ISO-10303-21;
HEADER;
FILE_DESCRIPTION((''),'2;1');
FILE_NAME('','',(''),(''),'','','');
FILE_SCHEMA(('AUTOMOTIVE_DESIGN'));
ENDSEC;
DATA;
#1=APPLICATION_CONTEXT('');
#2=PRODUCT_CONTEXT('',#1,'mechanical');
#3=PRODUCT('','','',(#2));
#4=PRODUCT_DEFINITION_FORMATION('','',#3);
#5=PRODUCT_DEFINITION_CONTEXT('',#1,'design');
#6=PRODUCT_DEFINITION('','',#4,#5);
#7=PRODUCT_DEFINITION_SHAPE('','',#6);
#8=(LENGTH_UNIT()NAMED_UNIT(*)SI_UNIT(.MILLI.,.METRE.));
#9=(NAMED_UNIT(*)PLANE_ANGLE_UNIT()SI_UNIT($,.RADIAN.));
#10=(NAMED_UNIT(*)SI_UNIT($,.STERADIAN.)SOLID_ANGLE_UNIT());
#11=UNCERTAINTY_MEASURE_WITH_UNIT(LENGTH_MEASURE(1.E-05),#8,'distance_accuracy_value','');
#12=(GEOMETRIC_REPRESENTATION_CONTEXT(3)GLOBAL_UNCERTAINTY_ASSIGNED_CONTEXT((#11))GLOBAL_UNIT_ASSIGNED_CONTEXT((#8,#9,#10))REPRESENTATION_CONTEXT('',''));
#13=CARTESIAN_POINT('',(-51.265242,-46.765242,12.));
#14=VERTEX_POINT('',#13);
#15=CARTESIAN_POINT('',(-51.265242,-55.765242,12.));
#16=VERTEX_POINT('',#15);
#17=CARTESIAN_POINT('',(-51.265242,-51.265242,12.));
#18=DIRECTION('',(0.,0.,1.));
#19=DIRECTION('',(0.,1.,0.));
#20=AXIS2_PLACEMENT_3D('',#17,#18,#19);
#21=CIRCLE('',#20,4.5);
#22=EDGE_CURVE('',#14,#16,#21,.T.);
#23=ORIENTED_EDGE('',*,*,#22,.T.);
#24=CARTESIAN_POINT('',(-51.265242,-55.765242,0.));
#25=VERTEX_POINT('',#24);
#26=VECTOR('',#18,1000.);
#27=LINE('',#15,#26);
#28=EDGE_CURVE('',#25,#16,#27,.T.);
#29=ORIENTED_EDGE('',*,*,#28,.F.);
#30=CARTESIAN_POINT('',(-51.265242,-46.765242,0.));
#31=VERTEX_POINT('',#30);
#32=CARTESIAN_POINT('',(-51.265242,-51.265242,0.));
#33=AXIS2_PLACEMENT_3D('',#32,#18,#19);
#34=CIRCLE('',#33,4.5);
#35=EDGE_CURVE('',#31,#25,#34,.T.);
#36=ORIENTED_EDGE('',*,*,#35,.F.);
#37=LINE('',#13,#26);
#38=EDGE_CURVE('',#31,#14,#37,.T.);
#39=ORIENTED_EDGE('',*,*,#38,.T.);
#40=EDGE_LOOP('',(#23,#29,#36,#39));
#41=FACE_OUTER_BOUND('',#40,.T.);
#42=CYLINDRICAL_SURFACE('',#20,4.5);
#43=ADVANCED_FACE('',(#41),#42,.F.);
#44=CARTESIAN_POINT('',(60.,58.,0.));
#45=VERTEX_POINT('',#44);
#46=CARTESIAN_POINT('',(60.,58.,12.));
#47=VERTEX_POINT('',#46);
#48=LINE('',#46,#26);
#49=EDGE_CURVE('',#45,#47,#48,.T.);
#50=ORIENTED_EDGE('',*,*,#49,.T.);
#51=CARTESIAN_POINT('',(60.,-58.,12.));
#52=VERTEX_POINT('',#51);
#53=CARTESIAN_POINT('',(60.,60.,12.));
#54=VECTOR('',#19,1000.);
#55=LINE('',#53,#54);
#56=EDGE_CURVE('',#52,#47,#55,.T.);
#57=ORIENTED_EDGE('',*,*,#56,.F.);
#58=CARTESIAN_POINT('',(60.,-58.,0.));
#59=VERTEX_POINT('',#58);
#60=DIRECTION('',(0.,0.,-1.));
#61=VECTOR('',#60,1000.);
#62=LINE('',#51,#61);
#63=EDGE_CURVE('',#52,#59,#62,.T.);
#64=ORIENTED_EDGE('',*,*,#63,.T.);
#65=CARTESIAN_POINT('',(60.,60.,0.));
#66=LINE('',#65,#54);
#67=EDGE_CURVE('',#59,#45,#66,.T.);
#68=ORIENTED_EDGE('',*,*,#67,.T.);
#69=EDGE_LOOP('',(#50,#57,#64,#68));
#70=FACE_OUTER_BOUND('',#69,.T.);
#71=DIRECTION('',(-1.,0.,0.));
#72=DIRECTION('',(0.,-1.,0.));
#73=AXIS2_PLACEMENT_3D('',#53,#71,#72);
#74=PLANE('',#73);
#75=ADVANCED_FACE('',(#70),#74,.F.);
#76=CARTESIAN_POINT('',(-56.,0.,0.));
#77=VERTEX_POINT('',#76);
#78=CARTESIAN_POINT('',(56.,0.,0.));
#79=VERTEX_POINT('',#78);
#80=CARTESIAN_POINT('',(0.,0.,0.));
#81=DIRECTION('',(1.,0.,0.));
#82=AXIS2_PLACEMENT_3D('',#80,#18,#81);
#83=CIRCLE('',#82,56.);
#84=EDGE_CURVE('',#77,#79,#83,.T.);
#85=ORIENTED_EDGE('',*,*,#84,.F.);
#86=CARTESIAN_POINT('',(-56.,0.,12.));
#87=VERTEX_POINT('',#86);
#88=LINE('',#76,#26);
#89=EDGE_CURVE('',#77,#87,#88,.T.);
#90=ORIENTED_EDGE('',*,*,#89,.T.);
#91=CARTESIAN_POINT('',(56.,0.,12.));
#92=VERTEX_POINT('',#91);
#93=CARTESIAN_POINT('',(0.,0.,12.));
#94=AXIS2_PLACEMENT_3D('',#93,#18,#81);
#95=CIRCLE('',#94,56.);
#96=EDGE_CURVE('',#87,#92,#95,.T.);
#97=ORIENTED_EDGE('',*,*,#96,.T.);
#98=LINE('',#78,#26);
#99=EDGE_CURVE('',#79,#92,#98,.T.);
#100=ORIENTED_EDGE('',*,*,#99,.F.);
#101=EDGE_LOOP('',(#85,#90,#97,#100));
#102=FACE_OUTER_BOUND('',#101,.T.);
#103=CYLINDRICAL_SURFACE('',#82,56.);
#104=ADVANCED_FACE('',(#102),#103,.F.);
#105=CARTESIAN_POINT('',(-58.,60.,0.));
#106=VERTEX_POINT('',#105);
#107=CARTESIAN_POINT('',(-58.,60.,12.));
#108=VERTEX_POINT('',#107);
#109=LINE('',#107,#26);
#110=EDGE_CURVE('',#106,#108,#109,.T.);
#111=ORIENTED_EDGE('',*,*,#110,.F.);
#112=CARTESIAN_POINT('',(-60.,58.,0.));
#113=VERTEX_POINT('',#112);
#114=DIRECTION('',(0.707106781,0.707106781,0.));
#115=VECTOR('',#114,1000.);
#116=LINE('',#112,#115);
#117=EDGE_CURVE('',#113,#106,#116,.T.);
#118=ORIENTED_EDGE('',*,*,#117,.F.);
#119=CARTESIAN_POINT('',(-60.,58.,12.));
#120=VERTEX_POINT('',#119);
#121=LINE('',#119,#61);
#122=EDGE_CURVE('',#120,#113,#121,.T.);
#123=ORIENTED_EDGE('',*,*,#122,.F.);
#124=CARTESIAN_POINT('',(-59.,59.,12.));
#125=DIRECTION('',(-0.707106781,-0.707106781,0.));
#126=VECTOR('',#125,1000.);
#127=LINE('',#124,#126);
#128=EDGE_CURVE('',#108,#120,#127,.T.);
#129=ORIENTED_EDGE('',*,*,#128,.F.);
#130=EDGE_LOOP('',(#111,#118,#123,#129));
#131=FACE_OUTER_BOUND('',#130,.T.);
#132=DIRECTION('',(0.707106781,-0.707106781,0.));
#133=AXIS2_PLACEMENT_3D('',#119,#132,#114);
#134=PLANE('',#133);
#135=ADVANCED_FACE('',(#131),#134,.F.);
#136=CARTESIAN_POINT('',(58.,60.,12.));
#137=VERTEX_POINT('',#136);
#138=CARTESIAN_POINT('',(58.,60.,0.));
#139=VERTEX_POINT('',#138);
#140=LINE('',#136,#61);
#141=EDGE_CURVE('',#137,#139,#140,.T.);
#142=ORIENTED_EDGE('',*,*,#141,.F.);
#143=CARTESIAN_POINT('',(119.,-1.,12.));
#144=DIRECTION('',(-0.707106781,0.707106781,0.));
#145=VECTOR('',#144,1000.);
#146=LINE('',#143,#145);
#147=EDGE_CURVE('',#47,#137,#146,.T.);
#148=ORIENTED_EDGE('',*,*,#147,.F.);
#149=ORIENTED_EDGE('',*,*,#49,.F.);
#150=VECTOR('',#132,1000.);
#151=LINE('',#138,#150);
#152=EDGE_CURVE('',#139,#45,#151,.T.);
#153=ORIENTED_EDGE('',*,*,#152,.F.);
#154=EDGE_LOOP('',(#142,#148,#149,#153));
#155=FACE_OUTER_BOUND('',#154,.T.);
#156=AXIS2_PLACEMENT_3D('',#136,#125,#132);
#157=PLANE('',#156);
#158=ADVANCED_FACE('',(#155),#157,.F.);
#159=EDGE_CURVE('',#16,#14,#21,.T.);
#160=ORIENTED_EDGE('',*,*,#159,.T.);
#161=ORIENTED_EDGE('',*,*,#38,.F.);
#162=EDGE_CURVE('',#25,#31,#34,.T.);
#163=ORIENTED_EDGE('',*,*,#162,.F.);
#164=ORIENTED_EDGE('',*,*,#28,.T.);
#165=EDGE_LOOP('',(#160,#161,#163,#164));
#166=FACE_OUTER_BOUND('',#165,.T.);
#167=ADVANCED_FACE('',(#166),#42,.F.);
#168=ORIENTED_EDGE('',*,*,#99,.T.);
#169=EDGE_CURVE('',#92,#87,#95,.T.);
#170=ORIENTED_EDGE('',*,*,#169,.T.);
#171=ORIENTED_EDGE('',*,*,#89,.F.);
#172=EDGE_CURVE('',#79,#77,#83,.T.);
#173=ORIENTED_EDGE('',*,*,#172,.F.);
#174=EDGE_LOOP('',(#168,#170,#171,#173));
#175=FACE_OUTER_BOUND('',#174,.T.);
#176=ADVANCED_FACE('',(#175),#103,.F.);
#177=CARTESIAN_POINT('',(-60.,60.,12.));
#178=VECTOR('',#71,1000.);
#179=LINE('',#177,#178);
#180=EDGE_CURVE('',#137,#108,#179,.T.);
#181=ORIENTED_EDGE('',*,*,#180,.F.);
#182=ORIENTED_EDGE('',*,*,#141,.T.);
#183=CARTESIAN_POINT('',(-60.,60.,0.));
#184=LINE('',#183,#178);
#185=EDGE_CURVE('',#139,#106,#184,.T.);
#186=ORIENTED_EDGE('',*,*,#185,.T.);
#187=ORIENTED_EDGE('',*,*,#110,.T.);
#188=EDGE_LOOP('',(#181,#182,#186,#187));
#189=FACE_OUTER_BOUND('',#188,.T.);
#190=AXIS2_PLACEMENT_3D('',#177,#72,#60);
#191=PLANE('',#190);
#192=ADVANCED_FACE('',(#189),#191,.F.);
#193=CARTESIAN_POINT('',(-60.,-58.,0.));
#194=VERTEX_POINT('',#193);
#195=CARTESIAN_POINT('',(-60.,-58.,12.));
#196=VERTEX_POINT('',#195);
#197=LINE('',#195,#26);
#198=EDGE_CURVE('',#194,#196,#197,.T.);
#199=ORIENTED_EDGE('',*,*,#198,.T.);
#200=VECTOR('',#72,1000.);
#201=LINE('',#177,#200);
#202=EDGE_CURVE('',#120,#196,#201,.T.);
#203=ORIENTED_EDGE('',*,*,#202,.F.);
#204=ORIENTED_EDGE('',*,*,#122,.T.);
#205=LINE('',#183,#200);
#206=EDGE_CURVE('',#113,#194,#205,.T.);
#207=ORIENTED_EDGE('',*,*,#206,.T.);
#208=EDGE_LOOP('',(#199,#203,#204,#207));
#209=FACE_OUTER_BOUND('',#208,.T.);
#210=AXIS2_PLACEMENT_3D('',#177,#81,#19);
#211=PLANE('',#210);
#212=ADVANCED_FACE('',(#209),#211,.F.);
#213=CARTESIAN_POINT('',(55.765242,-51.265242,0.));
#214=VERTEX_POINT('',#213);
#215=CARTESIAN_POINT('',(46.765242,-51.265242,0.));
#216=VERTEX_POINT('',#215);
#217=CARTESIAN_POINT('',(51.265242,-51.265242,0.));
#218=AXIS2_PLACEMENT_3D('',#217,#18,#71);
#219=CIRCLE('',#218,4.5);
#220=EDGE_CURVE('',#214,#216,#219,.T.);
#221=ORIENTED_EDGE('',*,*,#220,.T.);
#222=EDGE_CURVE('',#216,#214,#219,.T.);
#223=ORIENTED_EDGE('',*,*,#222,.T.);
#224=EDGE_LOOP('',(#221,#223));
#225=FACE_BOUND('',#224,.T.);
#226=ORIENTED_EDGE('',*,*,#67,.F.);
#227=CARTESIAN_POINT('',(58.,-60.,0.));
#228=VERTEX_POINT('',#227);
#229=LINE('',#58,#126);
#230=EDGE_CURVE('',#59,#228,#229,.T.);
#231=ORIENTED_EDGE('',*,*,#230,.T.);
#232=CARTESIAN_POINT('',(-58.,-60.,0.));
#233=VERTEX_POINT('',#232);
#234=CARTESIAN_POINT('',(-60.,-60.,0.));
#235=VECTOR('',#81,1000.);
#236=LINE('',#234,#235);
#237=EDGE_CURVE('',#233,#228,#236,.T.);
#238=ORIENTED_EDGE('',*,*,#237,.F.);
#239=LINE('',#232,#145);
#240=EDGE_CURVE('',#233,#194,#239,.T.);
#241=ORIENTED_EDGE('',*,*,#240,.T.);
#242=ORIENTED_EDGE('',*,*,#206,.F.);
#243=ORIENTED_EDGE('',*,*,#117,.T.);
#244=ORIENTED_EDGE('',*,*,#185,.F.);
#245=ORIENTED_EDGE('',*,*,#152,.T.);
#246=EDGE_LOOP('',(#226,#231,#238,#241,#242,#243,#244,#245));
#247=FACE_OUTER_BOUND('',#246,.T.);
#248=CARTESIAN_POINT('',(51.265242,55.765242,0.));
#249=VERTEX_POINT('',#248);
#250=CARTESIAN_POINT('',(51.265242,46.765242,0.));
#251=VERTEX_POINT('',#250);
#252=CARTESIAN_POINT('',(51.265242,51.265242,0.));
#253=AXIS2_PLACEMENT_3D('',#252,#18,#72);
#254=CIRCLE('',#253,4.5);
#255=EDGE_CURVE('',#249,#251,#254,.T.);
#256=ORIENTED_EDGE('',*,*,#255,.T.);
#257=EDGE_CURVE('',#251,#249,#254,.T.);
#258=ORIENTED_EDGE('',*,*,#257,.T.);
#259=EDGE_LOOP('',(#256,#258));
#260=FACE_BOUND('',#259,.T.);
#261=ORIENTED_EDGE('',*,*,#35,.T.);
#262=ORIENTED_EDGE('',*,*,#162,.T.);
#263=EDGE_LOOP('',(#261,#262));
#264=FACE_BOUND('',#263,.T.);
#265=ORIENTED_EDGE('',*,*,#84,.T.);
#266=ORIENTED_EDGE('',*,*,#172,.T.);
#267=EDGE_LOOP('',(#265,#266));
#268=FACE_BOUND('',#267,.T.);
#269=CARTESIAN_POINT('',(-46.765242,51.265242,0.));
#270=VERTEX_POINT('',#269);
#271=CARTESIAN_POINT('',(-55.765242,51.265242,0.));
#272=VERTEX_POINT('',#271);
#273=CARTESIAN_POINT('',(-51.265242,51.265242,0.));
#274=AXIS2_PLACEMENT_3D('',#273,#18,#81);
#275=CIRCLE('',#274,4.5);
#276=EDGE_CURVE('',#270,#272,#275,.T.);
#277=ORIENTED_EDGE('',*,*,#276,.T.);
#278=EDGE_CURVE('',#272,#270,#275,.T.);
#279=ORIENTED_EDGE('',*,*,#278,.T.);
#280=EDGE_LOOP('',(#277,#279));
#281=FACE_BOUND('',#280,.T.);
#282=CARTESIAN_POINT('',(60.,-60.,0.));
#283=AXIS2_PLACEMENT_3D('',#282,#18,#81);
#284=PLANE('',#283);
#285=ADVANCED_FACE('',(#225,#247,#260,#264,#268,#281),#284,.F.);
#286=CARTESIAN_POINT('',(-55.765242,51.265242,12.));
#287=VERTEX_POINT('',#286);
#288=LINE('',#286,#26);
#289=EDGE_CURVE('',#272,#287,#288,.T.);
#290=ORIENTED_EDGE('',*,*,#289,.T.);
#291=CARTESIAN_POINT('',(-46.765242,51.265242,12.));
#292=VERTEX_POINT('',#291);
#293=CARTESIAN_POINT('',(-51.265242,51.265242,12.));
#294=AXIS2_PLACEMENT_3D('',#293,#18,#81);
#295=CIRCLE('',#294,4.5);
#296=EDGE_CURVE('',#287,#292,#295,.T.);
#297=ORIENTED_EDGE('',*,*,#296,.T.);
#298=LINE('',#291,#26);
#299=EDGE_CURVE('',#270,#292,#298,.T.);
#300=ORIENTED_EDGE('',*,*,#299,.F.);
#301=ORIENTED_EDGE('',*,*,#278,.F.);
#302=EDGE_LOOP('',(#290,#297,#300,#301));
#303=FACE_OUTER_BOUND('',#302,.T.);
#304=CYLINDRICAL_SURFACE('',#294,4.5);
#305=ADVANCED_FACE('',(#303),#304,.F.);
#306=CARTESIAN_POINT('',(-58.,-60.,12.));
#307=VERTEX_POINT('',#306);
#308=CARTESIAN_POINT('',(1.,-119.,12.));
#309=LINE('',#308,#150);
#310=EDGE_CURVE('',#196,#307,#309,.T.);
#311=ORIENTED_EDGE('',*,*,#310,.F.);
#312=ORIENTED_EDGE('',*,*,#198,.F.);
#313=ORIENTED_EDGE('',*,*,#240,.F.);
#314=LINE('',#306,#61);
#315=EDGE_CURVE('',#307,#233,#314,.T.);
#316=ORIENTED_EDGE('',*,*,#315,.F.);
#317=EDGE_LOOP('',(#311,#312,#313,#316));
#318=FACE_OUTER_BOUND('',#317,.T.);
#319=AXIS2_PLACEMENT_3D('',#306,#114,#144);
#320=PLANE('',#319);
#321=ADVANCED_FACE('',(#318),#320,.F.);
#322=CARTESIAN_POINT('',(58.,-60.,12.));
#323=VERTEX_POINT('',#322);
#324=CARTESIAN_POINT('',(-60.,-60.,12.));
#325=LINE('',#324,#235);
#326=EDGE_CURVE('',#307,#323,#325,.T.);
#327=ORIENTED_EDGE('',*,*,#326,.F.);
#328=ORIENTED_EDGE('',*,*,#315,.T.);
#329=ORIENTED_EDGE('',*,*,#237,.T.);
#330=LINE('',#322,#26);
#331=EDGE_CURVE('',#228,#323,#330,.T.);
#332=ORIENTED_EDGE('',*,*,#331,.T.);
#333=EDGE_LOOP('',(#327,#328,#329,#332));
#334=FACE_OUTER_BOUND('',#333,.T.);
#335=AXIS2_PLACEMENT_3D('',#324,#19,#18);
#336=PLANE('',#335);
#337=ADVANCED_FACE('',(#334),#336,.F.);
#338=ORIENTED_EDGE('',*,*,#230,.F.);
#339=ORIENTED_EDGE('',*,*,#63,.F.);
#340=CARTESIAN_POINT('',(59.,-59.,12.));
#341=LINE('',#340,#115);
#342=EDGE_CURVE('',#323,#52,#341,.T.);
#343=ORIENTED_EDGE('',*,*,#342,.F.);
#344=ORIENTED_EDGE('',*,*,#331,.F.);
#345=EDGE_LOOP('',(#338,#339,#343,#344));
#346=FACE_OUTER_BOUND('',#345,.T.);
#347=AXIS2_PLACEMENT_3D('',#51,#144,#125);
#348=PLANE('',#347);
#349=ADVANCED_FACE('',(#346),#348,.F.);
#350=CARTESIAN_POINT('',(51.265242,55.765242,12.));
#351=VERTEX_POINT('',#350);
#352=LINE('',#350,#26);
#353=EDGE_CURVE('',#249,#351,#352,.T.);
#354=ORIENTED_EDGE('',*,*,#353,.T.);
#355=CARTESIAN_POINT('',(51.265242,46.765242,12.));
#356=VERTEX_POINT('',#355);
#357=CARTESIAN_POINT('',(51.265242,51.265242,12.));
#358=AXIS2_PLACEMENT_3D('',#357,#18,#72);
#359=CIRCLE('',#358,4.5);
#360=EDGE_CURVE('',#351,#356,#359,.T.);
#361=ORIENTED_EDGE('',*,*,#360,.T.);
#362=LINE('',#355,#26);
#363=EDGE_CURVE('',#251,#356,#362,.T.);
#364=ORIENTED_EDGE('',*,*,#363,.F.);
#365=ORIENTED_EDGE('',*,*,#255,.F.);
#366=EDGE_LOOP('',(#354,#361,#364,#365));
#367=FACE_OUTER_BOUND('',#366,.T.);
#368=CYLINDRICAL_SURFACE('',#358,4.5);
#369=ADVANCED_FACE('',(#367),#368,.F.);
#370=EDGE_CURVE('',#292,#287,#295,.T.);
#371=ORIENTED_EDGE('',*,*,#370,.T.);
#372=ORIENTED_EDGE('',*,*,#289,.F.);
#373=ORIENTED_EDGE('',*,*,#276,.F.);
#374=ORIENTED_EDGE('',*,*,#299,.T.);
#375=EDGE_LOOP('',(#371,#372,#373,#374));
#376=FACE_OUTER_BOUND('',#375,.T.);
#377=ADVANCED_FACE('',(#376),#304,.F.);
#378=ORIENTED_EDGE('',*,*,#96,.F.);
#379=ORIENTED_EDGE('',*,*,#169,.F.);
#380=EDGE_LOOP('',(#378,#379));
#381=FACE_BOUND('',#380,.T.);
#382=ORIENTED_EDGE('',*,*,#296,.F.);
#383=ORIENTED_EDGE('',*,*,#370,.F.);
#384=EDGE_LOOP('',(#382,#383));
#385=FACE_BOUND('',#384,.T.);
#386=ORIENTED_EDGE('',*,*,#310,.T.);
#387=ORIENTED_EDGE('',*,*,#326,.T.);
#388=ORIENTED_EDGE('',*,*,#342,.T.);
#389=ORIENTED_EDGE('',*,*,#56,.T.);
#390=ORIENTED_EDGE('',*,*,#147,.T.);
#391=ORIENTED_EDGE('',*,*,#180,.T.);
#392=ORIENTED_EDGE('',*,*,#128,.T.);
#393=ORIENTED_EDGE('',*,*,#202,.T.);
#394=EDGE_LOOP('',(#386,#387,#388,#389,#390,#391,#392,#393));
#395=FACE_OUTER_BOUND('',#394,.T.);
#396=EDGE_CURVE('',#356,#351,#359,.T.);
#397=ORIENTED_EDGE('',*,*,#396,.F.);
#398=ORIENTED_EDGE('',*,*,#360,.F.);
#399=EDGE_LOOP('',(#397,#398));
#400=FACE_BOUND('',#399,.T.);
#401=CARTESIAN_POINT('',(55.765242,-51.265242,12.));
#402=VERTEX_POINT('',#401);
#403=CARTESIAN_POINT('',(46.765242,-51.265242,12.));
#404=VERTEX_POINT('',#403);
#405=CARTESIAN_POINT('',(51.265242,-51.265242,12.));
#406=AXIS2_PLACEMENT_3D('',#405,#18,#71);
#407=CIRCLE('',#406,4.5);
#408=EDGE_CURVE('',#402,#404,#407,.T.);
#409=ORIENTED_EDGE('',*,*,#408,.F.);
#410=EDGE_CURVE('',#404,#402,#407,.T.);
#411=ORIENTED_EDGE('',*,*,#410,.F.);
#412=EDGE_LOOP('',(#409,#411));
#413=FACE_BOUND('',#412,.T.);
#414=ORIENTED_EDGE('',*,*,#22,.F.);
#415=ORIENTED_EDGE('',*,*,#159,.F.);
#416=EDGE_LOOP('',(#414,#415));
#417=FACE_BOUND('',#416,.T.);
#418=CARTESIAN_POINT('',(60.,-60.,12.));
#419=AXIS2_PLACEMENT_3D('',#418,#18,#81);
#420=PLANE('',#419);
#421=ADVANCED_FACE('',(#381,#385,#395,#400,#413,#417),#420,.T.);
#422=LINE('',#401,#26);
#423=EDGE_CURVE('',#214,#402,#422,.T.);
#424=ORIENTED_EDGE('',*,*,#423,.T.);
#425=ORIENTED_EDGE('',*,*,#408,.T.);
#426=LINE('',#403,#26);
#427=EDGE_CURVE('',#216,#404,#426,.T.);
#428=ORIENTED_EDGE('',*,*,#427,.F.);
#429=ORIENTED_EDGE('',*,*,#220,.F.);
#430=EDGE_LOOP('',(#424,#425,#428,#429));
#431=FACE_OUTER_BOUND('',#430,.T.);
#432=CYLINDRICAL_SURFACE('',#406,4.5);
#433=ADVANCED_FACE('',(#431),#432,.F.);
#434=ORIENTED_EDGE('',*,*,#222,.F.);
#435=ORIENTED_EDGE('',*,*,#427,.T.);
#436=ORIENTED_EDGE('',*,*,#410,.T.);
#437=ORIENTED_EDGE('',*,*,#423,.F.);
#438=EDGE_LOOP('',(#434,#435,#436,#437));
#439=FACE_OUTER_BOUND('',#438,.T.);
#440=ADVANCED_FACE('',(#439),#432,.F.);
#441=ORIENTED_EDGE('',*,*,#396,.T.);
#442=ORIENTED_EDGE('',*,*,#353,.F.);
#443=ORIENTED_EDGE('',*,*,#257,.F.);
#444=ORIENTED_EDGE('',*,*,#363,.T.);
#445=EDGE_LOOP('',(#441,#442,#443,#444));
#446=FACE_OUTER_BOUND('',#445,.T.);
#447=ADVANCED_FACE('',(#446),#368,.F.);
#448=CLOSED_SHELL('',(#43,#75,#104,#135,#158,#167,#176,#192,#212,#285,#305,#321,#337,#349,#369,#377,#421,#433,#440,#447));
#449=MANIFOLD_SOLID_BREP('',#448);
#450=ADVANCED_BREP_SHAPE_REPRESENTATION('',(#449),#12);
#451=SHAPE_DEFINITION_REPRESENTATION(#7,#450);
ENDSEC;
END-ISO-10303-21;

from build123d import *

# Parameters (mm, degrees)
SKETCH1_W           = 120
SKETCH1_H           = 120
BOSS_EXTRUDE1_DEPTH = 12
SKETCH2_R           = 56
CUT_EXTRUDE1_DEPTH  = 86.697141143
CIRPATTERN1_COUNT   = 4
CHAMFER1_SIZE       = 2


with BuildPart() as part:
    # Sketch1 → Boss-Extrude1 (new body)
    with BuildSketch(Plane.XY):
        Rectangle(SKETCH1_W, SKETCH1_H)
    extrude(amount=BOSS_EXTRUDE1_DEPTH)

    # Sketch2 → Cut-Extrude1 (cut, through all)
    with BuildSketch(Plane.XY.offset(12)):
        Circle(SKETCH2_R)
    extrude(amount=-CUT_EXTRUDE1_DEPTH, mode=Mode.SUBTRACT)

    # Sketch3 → M8 Clearance Hole1 (revolve, cut)
    with BuildSketch(Plane(origin=(-51.265241636, 51.265241636, 12), x_dir=(0, -1, 0), z_dir=(1, 0, 0))):
        Polygon((0, 0), (0, 52.703872786), (4.5, 50), (4.5, 0), align=None)
    m8_clearance_hole1 = revolve(axis=Axis((-51.265241636, 51.265241636, 18.35), (0, 0, -1)), mode=Mode.SUBTRACT)

    # CirPattern1: M8 Clearance Hole1 ×4 about axis
    cirpattern1_axis = Axis((0, 0, 0), (0, 0, 1))
    for i in range(1, CIRPATTERN1_COUNT):
        add(m8_clearance_hole1.rotate(cirpattern1_axis, i * 360 / CIRPATTERN1_COUNT), mode=Mode.SUBTRACT)

    # Chamfer1
    chamfer1_edges = [part.edges().sort_by_distance(p)[0] for p in [
        (60, -60, 6),
        (-60, -60, 6),
        (-60, 60, 6),
        (60, 60, 6),
    ]]
    chamfer(chamfer1_edges, length=CHAMFER1_SIZE)


solid = part.part
